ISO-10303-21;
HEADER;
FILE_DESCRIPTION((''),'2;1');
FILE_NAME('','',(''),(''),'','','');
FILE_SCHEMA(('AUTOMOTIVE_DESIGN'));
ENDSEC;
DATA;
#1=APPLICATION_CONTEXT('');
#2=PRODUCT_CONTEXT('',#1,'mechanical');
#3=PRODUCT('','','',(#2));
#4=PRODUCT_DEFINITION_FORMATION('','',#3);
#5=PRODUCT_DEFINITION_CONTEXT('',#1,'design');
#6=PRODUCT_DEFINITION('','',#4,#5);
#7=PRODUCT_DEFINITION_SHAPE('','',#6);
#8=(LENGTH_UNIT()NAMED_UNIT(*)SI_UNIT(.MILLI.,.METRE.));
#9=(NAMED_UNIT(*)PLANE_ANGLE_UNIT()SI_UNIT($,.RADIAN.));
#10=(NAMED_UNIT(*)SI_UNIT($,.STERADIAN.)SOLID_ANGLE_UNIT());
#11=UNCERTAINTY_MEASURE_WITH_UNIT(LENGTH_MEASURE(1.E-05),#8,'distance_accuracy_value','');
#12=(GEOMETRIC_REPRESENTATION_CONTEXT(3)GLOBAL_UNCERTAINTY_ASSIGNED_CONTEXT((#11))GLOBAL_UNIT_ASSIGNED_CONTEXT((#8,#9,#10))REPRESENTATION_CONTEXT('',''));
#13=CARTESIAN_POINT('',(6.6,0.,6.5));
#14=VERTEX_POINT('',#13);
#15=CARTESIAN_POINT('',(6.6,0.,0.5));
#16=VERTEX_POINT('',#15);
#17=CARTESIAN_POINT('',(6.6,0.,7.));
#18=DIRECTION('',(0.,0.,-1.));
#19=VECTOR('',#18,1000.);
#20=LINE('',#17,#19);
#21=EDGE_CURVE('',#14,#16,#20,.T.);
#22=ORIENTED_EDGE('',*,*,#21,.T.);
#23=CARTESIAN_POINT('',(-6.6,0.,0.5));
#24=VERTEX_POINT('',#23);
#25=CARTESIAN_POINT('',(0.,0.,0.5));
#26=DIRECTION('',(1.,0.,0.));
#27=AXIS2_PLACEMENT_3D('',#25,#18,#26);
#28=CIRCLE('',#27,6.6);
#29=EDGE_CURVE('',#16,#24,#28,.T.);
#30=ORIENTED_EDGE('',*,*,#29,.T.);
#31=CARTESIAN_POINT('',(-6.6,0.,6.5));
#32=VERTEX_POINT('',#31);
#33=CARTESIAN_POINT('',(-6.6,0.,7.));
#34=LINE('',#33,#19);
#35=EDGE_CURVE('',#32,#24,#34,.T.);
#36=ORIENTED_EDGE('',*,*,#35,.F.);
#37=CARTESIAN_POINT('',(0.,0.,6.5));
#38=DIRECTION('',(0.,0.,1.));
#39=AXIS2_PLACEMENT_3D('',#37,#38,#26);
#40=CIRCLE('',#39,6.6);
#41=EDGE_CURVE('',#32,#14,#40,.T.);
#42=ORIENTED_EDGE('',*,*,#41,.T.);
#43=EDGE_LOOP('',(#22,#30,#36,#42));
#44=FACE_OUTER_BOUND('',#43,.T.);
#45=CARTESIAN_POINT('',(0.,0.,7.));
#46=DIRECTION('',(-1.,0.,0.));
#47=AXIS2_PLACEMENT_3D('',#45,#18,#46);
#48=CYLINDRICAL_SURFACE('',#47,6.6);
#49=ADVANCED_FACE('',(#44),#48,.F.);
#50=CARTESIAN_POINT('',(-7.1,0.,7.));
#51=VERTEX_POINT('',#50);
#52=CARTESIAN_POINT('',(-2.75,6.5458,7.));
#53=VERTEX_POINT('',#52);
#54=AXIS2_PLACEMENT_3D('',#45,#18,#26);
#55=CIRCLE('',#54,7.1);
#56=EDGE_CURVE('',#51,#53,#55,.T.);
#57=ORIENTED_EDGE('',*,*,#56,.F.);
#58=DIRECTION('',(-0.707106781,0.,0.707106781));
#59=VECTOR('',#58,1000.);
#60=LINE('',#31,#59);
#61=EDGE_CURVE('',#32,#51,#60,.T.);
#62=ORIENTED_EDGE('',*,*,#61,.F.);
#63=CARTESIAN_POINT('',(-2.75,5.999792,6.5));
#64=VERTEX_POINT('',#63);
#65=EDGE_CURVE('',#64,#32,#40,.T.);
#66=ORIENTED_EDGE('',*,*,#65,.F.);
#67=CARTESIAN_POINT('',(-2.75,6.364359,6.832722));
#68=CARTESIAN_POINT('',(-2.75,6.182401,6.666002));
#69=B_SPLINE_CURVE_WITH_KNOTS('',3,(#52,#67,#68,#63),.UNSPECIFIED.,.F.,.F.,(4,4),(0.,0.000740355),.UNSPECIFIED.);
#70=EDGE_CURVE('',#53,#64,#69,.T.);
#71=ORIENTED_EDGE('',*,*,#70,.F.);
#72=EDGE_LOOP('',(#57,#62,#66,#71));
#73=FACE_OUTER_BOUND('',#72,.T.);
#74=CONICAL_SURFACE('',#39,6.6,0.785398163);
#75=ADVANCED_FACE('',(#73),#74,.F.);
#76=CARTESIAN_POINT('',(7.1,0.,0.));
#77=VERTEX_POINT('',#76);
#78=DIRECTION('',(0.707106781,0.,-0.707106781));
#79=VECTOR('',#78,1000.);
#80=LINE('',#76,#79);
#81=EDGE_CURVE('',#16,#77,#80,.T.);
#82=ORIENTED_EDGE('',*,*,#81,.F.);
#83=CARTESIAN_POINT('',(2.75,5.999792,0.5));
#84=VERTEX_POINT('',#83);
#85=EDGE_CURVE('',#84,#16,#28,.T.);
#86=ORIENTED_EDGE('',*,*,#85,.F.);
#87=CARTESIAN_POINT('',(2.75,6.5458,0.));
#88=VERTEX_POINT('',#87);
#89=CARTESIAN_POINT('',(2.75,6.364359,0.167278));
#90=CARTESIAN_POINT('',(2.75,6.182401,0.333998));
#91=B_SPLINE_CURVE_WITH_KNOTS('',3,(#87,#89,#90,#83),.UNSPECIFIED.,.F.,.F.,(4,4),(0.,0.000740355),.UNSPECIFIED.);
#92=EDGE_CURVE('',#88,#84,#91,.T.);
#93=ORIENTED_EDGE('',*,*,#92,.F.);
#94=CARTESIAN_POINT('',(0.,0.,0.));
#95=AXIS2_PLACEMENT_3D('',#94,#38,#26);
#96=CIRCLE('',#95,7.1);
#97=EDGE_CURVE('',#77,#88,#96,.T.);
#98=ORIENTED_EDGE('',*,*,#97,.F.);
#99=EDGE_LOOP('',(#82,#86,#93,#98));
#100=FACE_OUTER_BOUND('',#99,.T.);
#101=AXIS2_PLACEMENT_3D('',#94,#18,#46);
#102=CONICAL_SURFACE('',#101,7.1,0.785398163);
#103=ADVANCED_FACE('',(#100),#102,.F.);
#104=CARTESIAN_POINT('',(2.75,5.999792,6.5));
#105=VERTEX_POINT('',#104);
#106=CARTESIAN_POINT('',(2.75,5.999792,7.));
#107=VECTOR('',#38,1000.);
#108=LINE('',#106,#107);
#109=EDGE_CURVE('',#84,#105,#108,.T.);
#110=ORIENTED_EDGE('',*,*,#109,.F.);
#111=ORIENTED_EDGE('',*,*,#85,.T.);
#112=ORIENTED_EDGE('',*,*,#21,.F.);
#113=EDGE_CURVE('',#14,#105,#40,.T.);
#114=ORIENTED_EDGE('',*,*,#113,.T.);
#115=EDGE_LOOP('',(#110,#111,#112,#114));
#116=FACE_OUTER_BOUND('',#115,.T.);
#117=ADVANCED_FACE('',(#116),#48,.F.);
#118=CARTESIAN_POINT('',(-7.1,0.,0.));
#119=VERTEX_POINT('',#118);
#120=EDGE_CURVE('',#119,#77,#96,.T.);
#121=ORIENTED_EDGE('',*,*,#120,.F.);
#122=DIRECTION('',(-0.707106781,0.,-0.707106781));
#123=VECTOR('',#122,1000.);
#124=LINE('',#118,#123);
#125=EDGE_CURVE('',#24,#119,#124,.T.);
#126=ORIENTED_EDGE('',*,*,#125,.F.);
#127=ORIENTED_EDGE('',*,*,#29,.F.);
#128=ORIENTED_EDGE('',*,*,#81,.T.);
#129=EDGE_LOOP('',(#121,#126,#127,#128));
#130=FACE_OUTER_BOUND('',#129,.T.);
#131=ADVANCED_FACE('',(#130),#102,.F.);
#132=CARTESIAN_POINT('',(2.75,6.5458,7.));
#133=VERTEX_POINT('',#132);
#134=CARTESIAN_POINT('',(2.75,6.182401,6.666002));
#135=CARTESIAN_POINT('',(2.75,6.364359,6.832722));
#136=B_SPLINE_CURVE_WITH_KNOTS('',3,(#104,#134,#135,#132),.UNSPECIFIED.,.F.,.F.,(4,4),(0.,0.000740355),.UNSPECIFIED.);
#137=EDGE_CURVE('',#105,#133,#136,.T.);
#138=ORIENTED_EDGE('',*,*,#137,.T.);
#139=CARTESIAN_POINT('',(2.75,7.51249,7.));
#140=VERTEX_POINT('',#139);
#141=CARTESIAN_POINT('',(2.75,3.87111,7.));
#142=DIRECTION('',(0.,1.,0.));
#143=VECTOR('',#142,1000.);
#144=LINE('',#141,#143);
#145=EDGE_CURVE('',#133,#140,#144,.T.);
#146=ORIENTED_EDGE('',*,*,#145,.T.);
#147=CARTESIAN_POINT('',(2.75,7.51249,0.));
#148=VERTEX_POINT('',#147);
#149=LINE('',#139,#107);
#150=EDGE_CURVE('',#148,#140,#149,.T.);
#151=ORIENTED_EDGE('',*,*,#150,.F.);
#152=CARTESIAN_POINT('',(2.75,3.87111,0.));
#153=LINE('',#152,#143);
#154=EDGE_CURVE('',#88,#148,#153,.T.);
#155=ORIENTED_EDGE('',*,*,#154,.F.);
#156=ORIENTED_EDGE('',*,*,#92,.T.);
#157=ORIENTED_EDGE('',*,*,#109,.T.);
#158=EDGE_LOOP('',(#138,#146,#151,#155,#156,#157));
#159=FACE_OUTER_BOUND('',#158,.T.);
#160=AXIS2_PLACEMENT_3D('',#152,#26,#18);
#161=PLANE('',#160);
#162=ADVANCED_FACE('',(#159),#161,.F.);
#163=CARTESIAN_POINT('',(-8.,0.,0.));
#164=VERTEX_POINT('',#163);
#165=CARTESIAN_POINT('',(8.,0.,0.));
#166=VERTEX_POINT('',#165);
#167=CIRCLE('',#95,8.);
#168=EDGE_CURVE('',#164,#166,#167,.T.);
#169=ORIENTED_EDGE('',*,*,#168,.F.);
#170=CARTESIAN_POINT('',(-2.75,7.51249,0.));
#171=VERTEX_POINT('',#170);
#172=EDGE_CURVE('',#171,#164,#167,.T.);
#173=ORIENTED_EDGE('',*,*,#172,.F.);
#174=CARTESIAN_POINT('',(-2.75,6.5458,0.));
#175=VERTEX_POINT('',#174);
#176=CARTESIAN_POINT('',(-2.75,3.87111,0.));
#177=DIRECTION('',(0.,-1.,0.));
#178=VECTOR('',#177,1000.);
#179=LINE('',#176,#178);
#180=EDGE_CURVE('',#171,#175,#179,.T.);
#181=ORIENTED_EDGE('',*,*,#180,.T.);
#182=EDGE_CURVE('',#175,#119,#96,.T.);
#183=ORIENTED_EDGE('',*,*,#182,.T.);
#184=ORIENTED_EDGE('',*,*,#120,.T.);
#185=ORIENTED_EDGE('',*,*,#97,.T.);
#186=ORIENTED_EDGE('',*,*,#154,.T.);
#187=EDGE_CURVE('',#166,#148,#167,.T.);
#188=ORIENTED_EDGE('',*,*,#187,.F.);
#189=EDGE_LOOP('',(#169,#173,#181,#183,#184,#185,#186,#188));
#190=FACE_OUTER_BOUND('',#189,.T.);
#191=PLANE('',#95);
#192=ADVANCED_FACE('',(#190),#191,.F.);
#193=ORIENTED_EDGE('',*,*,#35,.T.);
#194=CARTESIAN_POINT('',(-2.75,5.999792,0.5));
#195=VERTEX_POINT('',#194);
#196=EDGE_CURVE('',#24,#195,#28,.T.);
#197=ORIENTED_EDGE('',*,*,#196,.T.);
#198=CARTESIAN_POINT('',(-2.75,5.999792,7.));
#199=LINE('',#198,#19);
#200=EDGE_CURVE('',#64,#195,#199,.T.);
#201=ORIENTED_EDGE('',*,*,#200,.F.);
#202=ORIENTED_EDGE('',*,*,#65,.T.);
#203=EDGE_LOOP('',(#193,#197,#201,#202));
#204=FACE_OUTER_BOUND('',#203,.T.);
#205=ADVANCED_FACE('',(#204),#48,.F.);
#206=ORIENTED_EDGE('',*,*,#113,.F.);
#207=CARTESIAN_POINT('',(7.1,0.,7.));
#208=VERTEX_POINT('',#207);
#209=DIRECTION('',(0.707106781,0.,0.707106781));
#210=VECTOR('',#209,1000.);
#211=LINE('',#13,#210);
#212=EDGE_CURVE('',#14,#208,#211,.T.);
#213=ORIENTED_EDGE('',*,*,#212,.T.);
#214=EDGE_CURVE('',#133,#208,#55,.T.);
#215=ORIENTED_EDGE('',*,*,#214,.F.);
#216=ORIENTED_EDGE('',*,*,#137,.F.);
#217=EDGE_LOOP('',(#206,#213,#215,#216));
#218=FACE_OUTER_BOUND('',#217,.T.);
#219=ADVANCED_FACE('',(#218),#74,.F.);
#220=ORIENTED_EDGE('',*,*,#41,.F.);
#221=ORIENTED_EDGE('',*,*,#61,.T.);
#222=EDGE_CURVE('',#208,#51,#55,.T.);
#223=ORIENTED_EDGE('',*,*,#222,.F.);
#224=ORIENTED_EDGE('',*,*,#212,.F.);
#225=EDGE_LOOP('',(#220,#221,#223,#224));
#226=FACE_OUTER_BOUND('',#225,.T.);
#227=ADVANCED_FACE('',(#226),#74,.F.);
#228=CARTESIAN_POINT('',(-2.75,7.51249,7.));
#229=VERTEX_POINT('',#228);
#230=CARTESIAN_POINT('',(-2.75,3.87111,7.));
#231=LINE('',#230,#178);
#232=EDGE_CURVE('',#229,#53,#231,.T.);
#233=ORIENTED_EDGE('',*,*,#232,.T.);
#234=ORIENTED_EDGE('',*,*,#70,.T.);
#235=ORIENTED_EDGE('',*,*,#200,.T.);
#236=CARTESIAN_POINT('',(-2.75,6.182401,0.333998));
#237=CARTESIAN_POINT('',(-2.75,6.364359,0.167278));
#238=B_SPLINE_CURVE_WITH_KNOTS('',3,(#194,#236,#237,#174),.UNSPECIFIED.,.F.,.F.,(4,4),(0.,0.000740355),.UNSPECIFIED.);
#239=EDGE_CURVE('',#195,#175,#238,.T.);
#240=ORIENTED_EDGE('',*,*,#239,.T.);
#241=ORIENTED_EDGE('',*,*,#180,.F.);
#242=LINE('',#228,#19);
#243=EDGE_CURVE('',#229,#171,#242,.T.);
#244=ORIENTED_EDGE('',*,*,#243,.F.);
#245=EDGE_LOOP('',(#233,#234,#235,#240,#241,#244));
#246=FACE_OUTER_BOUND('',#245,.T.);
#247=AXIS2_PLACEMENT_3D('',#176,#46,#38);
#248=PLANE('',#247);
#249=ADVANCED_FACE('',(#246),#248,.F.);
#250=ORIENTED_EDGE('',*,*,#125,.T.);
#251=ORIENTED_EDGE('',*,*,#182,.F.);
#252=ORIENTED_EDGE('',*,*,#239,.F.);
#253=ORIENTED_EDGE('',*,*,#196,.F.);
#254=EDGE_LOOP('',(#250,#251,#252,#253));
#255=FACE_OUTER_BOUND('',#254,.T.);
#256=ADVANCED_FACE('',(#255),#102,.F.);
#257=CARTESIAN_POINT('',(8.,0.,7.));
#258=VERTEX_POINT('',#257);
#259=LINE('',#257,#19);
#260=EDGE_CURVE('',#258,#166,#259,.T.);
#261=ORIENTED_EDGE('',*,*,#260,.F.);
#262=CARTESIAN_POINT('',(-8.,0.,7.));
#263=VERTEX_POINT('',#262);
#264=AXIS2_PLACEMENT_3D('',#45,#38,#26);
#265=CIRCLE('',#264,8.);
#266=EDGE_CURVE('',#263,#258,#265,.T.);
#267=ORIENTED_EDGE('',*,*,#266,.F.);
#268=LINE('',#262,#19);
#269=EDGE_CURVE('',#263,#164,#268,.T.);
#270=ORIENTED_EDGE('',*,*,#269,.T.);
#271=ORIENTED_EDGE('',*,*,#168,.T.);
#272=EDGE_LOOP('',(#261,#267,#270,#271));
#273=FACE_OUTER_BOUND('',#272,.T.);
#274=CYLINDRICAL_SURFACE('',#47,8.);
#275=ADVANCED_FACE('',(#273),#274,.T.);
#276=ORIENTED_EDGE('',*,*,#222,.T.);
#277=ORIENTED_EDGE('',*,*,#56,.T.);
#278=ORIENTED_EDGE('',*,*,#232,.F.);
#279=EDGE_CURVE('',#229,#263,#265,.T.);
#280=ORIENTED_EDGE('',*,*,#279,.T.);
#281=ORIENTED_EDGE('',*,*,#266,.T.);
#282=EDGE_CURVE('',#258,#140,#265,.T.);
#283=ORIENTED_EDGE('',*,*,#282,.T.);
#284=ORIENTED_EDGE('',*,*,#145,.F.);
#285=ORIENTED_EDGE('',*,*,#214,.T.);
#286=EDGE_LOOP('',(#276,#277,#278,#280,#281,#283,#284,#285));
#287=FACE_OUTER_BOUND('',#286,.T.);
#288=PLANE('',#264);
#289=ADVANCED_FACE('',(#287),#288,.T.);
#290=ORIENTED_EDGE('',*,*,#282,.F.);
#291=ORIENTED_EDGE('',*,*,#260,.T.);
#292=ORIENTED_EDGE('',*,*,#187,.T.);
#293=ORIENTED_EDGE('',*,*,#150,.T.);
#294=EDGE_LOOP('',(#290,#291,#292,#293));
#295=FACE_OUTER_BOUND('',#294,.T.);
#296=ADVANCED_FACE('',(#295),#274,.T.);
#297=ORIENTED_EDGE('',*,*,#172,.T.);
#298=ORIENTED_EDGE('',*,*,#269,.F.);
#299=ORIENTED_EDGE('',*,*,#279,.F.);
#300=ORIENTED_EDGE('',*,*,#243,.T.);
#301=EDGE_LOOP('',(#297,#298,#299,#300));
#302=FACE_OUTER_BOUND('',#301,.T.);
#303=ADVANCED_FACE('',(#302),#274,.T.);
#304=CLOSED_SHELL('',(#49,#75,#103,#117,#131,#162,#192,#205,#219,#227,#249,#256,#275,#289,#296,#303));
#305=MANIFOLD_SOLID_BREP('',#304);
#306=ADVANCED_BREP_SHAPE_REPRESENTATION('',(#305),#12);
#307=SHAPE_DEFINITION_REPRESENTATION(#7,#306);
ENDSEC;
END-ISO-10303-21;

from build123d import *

# Parameters (mm, degrees)
SKETCH1_R           = 8
SKETCH1_R_2         = 6.6
BOSS_EXTRUDE1_DEPTH = 7
SKETCH2_W           = 5.5
SKETCH2_H           = 7.166353003
CUT_EXTRUDE1_DEPTH  = 14.304134696
CHAMFER1_SIZE       = 0.5


with BuildPart() as part:
    # Sketch1 → Boss-Extrude1 (new body)
    with BuildSketch(Plane.XY):
        Circle(SKETCH1_R)
        Circle(SKETCH1_R_2, mode=Mode.SUBTRACT)
    extrude(amount=BOSS_EXTRUDE1_DEPTH)

    # Sketch2 → Cut-Extrude1 (cut, through all)
    with BuildSketch(Plane.XY.offset(7)):
        with Locations((0, 7.454286829)):
            Rectangle(SKETCH2_W, SKETCH2_H)
    extrude(amount=-CUT_EXTRUDE1_DEPTH, mode=Mode.SUBTRACT)

    # Chamfer1
    chamfer1_edges = [part.edges().sort_by_distance(p)[0] for p in [
        (0, -6.6, 0),
        (0, -6.6, 7),
    ]]
    chamfer(chamfer1_edges, length=CHAMFER1_SIZE)


solid = part.part
